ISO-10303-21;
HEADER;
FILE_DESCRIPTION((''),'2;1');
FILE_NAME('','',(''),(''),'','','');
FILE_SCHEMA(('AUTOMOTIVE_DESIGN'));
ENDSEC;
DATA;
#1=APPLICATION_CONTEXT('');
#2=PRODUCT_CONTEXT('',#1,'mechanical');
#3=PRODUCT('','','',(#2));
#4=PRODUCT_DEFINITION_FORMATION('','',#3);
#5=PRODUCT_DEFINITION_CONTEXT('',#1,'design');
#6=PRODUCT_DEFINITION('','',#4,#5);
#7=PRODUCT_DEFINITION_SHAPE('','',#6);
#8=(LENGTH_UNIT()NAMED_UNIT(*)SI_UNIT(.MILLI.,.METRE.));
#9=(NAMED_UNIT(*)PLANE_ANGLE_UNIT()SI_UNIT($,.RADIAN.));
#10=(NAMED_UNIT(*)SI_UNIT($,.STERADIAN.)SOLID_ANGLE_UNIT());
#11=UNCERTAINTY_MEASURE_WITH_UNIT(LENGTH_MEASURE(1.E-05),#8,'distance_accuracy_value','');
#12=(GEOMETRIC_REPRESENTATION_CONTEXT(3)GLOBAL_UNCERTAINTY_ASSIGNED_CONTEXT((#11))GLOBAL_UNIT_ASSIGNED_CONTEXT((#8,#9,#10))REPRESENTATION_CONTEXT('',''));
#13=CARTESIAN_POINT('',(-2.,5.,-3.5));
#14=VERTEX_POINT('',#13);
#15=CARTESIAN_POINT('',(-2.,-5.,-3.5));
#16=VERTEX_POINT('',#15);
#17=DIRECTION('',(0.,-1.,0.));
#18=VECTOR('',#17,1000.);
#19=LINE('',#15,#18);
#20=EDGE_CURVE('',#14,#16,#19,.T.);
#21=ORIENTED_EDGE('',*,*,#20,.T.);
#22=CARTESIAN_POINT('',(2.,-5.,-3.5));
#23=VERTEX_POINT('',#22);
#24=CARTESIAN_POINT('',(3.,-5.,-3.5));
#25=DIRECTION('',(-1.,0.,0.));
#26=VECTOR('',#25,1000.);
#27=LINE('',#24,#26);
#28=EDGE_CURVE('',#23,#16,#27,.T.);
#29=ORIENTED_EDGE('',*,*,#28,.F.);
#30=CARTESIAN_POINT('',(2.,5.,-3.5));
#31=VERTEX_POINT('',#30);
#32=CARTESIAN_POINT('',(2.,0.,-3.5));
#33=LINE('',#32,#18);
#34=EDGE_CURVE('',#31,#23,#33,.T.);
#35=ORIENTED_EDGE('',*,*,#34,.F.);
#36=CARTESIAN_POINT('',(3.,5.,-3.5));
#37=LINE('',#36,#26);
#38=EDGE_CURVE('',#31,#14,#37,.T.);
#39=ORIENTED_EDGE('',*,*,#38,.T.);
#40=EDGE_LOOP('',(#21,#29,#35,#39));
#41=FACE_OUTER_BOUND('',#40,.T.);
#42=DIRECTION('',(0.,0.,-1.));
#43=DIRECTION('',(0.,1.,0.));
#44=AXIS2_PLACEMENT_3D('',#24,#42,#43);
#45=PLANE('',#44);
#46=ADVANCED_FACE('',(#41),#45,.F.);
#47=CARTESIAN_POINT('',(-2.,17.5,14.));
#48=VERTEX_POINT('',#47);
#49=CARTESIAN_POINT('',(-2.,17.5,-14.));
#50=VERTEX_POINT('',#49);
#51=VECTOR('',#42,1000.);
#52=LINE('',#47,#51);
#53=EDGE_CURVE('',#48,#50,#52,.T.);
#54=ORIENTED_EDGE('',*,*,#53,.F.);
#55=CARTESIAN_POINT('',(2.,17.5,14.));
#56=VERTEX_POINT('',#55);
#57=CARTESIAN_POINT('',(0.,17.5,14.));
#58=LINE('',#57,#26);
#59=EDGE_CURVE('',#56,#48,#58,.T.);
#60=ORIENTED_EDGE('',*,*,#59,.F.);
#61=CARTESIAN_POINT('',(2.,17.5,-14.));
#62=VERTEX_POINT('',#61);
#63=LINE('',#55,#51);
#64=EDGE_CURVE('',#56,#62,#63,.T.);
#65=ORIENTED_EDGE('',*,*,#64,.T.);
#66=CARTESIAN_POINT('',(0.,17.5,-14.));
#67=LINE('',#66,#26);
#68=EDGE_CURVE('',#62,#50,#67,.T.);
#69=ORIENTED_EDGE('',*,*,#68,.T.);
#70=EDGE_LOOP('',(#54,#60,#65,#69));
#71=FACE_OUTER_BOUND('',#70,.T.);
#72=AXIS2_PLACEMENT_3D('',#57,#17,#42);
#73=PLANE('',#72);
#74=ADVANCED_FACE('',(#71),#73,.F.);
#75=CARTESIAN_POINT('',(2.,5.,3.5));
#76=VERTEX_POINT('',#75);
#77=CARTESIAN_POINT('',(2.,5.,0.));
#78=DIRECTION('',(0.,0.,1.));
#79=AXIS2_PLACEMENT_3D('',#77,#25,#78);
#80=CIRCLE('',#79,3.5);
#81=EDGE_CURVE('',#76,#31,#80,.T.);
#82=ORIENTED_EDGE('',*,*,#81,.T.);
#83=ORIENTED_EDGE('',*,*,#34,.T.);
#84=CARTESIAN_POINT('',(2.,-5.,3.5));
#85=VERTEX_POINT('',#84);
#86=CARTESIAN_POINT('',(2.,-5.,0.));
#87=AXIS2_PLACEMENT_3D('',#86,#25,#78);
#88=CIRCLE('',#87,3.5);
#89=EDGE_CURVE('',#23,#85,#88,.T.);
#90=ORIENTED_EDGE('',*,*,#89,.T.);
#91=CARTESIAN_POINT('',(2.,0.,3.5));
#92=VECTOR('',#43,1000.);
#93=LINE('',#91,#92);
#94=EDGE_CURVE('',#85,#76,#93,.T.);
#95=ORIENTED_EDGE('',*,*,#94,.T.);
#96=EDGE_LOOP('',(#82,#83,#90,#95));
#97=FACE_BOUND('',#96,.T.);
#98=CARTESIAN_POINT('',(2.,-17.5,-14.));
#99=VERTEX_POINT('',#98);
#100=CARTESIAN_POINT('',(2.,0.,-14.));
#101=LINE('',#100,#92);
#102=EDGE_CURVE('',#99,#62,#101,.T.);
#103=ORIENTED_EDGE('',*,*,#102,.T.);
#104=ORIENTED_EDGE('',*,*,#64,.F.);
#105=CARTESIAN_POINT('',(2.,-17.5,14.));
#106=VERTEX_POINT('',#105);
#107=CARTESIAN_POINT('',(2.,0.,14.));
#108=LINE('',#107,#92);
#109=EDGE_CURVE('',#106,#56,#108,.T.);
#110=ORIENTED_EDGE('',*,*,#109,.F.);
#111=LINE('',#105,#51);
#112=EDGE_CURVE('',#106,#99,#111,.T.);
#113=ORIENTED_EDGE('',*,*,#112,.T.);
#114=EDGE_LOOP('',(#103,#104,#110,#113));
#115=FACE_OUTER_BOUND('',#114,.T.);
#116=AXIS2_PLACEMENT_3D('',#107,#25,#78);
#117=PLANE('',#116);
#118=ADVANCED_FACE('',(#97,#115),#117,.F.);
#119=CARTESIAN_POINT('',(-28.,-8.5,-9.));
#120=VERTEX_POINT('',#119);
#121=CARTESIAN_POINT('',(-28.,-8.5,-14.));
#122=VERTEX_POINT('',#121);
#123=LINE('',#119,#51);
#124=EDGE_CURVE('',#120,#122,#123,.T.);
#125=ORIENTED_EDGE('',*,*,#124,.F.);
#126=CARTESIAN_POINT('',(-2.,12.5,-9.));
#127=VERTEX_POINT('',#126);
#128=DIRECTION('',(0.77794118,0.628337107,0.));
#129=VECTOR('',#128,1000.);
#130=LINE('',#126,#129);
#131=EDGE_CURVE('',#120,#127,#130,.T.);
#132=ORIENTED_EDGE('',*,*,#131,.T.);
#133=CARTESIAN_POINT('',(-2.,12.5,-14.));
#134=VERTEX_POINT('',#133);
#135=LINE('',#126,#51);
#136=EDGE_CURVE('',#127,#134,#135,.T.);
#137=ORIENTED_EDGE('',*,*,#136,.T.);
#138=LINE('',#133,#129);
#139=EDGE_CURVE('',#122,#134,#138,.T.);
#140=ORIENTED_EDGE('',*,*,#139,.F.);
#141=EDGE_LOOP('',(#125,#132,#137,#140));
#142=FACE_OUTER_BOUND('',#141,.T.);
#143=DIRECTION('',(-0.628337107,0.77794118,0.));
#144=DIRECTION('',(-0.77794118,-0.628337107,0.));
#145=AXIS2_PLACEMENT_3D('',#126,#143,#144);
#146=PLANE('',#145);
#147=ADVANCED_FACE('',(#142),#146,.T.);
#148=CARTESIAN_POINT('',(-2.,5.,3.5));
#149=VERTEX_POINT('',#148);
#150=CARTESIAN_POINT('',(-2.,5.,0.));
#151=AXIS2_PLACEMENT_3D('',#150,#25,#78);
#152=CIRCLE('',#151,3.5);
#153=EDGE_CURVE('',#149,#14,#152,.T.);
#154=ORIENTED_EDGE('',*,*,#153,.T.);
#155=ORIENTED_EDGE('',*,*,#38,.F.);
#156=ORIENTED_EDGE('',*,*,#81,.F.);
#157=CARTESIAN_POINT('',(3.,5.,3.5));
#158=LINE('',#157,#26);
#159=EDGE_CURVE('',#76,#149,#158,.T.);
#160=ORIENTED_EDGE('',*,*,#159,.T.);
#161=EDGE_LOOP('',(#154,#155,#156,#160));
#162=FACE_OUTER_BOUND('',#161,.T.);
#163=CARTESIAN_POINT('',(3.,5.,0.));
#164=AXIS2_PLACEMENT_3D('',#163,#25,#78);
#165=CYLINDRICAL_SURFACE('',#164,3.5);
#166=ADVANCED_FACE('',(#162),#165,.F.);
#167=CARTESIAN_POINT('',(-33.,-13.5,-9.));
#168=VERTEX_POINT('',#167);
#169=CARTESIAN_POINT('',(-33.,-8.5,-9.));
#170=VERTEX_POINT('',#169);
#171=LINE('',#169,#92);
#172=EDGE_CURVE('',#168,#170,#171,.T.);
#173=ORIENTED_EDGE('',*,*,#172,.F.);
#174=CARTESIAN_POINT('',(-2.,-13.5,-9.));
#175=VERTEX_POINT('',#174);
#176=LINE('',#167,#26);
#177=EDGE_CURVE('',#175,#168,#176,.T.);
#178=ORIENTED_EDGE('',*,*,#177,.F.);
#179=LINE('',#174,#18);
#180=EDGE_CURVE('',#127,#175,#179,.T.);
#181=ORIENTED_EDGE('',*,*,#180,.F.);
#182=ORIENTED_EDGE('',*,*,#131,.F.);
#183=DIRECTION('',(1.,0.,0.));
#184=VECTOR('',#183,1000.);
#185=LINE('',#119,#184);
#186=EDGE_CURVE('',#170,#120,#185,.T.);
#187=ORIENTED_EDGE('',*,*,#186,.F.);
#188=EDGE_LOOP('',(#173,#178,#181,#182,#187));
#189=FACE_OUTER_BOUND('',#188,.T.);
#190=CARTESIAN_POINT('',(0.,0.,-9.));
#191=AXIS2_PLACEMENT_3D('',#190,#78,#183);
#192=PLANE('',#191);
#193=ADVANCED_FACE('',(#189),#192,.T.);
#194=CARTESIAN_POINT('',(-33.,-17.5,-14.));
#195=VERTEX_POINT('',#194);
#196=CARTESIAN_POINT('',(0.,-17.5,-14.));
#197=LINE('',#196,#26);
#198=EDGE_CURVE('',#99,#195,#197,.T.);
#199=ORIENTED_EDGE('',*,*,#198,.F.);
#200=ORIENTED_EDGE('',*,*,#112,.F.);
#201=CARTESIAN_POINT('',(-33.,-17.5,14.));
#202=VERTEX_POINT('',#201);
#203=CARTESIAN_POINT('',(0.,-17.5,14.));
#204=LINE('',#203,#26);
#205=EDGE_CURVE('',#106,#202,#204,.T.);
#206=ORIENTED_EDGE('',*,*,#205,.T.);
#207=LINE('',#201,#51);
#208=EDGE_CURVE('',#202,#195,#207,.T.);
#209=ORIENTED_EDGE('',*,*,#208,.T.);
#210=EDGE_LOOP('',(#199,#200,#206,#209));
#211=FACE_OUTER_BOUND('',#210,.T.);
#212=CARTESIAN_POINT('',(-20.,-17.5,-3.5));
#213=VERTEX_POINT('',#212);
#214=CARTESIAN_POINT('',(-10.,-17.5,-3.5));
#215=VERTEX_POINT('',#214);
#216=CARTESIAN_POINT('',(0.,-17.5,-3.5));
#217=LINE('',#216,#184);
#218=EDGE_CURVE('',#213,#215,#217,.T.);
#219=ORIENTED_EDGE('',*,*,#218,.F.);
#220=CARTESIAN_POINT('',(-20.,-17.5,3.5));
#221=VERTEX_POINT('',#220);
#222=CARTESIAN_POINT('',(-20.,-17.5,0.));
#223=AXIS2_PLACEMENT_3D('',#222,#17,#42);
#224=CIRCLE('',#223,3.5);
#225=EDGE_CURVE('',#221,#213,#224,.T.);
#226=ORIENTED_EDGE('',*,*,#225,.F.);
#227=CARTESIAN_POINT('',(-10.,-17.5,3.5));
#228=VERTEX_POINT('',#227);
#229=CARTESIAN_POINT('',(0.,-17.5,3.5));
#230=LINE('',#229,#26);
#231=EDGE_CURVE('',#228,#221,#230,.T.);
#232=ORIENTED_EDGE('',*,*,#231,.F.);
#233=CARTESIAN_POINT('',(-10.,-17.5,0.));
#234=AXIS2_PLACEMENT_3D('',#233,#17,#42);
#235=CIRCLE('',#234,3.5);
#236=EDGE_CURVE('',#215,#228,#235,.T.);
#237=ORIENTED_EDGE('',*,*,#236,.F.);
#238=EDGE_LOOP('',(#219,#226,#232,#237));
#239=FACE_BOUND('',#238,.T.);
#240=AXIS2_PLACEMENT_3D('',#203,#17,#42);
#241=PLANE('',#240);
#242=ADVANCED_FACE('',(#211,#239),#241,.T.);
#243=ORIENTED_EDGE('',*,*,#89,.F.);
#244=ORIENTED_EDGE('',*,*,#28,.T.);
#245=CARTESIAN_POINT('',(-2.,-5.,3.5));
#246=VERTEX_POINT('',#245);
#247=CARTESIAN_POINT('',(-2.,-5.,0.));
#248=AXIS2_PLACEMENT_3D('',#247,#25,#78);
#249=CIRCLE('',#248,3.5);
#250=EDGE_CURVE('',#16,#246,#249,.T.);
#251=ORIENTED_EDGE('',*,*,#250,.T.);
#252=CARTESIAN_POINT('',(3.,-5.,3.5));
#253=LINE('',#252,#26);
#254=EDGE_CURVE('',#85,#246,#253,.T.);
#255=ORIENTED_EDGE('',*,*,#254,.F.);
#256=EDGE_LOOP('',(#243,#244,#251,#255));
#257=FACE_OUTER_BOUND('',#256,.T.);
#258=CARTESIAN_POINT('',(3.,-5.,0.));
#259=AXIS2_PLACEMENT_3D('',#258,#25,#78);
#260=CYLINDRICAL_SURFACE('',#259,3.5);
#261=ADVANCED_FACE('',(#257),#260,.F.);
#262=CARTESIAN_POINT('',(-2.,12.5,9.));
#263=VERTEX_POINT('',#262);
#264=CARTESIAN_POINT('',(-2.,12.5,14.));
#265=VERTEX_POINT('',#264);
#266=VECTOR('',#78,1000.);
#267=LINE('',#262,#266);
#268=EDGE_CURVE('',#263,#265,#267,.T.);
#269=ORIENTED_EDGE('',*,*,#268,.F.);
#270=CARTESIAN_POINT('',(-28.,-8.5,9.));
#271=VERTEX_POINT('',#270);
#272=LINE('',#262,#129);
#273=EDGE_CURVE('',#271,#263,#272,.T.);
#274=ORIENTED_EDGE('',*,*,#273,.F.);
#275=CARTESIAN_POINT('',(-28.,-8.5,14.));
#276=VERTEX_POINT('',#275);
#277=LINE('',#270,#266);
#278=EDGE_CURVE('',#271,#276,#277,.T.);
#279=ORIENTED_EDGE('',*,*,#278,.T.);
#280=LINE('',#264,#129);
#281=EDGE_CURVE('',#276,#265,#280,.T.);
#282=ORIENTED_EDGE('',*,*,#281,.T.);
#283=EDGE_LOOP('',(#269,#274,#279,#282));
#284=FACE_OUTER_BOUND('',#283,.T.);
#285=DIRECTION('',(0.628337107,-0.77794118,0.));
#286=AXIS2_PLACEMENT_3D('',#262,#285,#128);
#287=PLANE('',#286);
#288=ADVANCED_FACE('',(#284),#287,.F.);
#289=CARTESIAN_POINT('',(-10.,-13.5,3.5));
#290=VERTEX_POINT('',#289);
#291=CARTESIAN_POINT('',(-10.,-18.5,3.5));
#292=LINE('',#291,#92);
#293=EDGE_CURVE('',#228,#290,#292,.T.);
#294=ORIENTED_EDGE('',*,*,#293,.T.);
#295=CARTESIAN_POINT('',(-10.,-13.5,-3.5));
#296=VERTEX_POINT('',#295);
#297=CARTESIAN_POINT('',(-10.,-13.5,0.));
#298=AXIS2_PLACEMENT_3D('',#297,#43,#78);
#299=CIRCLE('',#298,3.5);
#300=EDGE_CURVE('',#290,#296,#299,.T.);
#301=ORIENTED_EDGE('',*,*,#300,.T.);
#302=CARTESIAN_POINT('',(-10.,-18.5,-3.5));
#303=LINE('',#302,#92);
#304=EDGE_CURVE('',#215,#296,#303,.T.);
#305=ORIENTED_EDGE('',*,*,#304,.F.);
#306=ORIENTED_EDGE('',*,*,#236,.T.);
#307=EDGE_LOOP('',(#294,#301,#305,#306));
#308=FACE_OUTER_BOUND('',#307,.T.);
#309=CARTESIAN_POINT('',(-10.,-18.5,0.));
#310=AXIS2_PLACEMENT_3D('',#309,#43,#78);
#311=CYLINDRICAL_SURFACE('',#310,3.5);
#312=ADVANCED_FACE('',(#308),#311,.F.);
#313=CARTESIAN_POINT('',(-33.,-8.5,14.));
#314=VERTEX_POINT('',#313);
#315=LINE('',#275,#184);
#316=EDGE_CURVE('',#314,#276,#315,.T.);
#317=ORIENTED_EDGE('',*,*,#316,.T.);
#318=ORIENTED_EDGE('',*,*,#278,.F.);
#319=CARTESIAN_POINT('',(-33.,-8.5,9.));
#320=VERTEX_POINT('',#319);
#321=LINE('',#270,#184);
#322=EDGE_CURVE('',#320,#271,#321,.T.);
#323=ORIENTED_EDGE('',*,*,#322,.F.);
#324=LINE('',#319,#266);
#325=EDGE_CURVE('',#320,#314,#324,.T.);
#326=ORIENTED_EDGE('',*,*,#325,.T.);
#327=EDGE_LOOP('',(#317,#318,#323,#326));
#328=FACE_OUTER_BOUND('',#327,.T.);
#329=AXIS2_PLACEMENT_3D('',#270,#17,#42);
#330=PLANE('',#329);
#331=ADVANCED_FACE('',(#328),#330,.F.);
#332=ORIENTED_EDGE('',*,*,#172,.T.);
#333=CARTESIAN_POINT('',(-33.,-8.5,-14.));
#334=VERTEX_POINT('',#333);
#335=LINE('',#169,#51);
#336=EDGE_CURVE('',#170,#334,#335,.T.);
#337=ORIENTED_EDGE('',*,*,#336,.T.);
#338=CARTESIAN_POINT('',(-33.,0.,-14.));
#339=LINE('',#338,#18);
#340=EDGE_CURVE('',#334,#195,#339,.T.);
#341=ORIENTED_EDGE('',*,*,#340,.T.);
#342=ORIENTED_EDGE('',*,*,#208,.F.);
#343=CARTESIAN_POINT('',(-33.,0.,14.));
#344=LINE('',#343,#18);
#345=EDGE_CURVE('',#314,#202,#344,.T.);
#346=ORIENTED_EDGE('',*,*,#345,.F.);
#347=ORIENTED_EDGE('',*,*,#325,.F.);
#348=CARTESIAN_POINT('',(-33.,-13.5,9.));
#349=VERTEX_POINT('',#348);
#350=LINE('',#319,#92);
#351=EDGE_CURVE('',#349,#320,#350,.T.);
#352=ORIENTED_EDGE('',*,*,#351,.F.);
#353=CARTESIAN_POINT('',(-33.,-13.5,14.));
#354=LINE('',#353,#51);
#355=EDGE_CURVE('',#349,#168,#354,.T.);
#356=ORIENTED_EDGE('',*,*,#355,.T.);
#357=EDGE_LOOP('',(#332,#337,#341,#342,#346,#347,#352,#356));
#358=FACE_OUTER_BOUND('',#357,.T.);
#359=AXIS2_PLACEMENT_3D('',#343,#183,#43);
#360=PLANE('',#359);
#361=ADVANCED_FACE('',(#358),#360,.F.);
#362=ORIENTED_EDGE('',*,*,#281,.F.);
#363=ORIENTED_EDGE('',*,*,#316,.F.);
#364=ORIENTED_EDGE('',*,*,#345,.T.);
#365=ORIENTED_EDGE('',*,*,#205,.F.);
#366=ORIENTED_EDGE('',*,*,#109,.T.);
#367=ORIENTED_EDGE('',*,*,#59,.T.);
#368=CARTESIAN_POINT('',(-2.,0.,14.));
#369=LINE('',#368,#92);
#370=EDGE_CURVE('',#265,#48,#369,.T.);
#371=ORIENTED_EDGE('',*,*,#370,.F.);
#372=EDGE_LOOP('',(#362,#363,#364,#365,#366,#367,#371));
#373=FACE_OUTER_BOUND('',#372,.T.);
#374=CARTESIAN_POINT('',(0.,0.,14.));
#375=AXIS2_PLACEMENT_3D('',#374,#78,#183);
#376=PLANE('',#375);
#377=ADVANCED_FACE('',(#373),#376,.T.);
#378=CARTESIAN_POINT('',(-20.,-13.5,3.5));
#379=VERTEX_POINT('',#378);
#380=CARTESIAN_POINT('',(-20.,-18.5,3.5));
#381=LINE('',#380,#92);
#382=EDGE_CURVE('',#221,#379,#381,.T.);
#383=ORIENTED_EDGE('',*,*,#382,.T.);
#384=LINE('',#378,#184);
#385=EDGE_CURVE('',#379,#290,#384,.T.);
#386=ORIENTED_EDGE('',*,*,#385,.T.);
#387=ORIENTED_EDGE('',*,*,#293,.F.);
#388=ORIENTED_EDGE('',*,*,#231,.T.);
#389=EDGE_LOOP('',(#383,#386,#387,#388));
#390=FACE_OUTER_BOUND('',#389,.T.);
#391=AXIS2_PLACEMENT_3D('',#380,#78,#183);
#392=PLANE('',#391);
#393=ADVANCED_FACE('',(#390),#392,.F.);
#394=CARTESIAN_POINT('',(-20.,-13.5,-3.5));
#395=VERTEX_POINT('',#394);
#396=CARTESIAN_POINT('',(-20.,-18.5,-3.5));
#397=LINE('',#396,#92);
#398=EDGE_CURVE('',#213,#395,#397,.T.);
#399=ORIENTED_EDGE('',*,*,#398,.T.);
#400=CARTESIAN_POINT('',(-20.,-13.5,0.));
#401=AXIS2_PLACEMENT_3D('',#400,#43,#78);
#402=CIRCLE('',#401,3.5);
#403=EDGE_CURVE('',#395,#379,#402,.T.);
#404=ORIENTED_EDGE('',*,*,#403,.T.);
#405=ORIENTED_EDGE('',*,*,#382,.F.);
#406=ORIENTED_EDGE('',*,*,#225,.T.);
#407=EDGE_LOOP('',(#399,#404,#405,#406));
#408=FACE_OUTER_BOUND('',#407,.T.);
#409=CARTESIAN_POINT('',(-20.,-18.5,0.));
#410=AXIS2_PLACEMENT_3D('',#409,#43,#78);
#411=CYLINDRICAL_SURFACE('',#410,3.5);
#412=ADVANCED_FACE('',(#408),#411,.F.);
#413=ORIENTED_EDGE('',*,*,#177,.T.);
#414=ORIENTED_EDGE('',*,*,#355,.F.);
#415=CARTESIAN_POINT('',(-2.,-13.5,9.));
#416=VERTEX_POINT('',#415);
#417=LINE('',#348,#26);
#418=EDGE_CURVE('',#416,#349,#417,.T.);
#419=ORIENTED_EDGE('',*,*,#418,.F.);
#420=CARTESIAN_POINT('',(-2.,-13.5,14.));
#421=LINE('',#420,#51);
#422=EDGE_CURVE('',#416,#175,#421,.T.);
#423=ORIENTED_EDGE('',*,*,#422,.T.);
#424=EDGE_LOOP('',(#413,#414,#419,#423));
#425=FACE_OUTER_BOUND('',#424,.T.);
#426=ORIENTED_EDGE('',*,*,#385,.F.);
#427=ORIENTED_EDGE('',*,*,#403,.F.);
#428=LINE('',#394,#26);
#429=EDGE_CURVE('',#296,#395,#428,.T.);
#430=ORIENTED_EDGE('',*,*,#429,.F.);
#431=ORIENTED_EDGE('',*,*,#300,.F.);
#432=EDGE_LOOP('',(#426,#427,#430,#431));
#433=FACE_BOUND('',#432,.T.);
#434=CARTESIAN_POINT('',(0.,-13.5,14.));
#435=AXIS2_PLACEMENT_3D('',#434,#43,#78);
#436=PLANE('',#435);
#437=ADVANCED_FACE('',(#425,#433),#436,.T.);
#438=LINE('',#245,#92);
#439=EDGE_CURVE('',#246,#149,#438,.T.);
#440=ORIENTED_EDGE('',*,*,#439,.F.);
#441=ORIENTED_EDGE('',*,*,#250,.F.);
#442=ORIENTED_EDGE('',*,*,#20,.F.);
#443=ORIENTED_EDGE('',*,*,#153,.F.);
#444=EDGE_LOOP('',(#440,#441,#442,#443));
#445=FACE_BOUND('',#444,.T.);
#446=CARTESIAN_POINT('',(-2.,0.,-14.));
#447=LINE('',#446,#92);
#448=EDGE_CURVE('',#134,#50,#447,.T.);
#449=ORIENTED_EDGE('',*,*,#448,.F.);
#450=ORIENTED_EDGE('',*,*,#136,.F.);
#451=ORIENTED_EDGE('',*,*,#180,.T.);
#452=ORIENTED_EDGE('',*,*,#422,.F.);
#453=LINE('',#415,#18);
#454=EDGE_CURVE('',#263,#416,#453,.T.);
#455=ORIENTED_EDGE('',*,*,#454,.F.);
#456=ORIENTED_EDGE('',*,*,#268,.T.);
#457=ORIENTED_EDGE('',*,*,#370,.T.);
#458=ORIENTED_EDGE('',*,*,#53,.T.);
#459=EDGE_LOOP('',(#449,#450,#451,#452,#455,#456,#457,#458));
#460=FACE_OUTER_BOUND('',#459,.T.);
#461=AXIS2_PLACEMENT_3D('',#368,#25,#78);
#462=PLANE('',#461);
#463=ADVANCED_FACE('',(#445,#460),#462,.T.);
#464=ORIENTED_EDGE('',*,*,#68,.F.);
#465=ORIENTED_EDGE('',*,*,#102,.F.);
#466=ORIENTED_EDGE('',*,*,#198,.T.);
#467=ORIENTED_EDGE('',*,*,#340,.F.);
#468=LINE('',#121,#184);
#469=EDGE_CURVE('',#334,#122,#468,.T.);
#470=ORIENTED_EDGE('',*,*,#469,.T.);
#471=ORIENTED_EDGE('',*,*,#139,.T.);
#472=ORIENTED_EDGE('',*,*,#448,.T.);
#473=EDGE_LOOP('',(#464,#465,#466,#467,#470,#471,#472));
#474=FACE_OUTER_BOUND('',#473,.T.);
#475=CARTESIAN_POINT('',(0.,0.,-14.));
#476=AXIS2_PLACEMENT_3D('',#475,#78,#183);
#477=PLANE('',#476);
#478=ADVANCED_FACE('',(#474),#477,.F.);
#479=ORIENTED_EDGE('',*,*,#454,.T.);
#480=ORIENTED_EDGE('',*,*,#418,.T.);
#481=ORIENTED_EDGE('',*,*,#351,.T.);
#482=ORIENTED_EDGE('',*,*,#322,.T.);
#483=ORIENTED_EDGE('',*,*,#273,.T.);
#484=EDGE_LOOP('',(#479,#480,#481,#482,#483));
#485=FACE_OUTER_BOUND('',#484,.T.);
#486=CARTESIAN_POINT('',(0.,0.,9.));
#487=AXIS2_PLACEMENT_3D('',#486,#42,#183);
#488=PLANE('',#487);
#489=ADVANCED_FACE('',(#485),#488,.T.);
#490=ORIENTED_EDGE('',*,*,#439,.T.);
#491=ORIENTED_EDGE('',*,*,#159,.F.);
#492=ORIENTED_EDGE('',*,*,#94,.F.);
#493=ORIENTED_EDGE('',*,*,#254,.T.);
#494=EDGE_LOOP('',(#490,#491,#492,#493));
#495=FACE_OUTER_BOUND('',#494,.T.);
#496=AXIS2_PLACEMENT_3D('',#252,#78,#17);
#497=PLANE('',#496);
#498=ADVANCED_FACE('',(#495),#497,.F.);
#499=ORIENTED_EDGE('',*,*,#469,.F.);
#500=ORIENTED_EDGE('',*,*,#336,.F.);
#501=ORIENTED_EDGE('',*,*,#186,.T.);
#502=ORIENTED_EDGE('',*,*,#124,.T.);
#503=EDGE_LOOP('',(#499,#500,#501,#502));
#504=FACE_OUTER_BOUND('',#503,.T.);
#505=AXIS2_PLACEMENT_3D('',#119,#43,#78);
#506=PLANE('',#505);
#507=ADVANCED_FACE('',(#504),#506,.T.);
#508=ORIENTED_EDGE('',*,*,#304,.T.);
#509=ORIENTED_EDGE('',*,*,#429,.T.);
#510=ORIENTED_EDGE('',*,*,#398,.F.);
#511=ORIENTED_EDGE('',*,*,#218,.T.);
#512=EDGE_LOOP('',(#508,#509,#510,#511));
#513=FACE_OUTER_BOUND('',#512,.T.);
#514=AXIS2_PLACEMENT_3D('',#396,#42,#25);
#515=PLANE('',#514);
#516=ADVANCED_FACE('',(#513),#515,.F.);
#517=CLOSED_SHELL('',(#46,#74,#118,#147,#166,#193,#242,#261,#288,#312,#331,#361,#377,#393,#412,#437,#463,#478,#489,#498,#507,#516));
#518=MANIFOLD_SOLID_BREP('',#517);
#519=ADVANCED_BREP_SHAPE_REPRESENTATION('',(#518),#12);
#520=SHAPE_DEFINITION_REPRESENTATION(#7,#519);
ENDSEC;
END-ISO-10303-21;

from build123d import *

# Parameters (mm, degrees)
SKETCH_1_W          = 4
SKETCH_1_H          = 31
SKETCH_1_H_2        = 4
SKETCH_1_W_2        = 31
EXTRUDE_1_DEPTH     = 14
EXTRUDE_2_DEPTH     = 5
CUT_EXTRUDE_1_DEPTH = 5
CUT_EXTRUDE_2_DEPTH = 5


with BuildPart() as part:
    # 草图1 → 凸台-拉伸1 (new, symmetric)
    with BuildSketch(Plane.XY):
        with Locations((0, 2)):
            Rectangle(SKETCH_1_W, SKETCH_1_H)
        with Locations((0, -15.5)):
            Rectangle(SKETCH_1_W, SKETCH_1_H_2)
        with Locations((-17.5, -15.5)):
            Rectangle(SKETCH_1_W_2, SKETCH_1_H_2)
    extrude(amount=EXTRUDE_1_DEPTH, both=True)

    # 草图2 → 凸台-拉伸2 (add)
    with BuildSketch(Plane(origin=(0, 0, -14), x_dir=(-1, 0, 0), z_dir=(0, 0, -1))):
        Polygon((2, 12.5), (28, -8.5), (33, -8.5), (33, -13.5), (2, -13.5), align=None)
    extrude_2 = extrude(amount=-EXTRUDE_2_DEPTH)

    # 镜向1: 凸台-拉伸2 across plane
    add(extrude_2.mirror(Plane.XY))

    # 草图3 → 切除-拉伸1 (cut)
    with BuildSketch(Plane.ZY.offset(2)):
        with BuildLine():
            Line((-3.5, -5), (-3.5, 5))
            ThreePointArc((-3.5, 5), (0, 8.5), (3.5, 5))
            Line((3.5, 5), (3.5, -5))
            ThreePointArc((3.5, -5), (0, -8.5), (-3.5, -5))
        make_face()
    extrude(amount=-CUT_EXTRUDE_1_DEPTH, mode=Mode.SUBTRACT)

    # 草图4 → 切除-拉伸2 (cut)
    with BuildSketch(Plane(origin=(0, -13.5, 0), x_dir=(1, 0, 0), z_dir=(0, 1, 0))):
        with BuildLine():
            Line((-20, 3.5), (-10, 3.5))
            ThreePointArc((-10, 3.5), (-6.5, 0), (-10, -3.5))
            Line((-10, -3.5), (-20, -3.5))
            ThreePointArc((-20, -3.5), (-23.5, 0), (-20, 3.5))
        make_face()
    extrude(amount=-CUT_EXTRUDE_2_DEPTH, mode=Mode.SUBTRACT)


solid = part.part
